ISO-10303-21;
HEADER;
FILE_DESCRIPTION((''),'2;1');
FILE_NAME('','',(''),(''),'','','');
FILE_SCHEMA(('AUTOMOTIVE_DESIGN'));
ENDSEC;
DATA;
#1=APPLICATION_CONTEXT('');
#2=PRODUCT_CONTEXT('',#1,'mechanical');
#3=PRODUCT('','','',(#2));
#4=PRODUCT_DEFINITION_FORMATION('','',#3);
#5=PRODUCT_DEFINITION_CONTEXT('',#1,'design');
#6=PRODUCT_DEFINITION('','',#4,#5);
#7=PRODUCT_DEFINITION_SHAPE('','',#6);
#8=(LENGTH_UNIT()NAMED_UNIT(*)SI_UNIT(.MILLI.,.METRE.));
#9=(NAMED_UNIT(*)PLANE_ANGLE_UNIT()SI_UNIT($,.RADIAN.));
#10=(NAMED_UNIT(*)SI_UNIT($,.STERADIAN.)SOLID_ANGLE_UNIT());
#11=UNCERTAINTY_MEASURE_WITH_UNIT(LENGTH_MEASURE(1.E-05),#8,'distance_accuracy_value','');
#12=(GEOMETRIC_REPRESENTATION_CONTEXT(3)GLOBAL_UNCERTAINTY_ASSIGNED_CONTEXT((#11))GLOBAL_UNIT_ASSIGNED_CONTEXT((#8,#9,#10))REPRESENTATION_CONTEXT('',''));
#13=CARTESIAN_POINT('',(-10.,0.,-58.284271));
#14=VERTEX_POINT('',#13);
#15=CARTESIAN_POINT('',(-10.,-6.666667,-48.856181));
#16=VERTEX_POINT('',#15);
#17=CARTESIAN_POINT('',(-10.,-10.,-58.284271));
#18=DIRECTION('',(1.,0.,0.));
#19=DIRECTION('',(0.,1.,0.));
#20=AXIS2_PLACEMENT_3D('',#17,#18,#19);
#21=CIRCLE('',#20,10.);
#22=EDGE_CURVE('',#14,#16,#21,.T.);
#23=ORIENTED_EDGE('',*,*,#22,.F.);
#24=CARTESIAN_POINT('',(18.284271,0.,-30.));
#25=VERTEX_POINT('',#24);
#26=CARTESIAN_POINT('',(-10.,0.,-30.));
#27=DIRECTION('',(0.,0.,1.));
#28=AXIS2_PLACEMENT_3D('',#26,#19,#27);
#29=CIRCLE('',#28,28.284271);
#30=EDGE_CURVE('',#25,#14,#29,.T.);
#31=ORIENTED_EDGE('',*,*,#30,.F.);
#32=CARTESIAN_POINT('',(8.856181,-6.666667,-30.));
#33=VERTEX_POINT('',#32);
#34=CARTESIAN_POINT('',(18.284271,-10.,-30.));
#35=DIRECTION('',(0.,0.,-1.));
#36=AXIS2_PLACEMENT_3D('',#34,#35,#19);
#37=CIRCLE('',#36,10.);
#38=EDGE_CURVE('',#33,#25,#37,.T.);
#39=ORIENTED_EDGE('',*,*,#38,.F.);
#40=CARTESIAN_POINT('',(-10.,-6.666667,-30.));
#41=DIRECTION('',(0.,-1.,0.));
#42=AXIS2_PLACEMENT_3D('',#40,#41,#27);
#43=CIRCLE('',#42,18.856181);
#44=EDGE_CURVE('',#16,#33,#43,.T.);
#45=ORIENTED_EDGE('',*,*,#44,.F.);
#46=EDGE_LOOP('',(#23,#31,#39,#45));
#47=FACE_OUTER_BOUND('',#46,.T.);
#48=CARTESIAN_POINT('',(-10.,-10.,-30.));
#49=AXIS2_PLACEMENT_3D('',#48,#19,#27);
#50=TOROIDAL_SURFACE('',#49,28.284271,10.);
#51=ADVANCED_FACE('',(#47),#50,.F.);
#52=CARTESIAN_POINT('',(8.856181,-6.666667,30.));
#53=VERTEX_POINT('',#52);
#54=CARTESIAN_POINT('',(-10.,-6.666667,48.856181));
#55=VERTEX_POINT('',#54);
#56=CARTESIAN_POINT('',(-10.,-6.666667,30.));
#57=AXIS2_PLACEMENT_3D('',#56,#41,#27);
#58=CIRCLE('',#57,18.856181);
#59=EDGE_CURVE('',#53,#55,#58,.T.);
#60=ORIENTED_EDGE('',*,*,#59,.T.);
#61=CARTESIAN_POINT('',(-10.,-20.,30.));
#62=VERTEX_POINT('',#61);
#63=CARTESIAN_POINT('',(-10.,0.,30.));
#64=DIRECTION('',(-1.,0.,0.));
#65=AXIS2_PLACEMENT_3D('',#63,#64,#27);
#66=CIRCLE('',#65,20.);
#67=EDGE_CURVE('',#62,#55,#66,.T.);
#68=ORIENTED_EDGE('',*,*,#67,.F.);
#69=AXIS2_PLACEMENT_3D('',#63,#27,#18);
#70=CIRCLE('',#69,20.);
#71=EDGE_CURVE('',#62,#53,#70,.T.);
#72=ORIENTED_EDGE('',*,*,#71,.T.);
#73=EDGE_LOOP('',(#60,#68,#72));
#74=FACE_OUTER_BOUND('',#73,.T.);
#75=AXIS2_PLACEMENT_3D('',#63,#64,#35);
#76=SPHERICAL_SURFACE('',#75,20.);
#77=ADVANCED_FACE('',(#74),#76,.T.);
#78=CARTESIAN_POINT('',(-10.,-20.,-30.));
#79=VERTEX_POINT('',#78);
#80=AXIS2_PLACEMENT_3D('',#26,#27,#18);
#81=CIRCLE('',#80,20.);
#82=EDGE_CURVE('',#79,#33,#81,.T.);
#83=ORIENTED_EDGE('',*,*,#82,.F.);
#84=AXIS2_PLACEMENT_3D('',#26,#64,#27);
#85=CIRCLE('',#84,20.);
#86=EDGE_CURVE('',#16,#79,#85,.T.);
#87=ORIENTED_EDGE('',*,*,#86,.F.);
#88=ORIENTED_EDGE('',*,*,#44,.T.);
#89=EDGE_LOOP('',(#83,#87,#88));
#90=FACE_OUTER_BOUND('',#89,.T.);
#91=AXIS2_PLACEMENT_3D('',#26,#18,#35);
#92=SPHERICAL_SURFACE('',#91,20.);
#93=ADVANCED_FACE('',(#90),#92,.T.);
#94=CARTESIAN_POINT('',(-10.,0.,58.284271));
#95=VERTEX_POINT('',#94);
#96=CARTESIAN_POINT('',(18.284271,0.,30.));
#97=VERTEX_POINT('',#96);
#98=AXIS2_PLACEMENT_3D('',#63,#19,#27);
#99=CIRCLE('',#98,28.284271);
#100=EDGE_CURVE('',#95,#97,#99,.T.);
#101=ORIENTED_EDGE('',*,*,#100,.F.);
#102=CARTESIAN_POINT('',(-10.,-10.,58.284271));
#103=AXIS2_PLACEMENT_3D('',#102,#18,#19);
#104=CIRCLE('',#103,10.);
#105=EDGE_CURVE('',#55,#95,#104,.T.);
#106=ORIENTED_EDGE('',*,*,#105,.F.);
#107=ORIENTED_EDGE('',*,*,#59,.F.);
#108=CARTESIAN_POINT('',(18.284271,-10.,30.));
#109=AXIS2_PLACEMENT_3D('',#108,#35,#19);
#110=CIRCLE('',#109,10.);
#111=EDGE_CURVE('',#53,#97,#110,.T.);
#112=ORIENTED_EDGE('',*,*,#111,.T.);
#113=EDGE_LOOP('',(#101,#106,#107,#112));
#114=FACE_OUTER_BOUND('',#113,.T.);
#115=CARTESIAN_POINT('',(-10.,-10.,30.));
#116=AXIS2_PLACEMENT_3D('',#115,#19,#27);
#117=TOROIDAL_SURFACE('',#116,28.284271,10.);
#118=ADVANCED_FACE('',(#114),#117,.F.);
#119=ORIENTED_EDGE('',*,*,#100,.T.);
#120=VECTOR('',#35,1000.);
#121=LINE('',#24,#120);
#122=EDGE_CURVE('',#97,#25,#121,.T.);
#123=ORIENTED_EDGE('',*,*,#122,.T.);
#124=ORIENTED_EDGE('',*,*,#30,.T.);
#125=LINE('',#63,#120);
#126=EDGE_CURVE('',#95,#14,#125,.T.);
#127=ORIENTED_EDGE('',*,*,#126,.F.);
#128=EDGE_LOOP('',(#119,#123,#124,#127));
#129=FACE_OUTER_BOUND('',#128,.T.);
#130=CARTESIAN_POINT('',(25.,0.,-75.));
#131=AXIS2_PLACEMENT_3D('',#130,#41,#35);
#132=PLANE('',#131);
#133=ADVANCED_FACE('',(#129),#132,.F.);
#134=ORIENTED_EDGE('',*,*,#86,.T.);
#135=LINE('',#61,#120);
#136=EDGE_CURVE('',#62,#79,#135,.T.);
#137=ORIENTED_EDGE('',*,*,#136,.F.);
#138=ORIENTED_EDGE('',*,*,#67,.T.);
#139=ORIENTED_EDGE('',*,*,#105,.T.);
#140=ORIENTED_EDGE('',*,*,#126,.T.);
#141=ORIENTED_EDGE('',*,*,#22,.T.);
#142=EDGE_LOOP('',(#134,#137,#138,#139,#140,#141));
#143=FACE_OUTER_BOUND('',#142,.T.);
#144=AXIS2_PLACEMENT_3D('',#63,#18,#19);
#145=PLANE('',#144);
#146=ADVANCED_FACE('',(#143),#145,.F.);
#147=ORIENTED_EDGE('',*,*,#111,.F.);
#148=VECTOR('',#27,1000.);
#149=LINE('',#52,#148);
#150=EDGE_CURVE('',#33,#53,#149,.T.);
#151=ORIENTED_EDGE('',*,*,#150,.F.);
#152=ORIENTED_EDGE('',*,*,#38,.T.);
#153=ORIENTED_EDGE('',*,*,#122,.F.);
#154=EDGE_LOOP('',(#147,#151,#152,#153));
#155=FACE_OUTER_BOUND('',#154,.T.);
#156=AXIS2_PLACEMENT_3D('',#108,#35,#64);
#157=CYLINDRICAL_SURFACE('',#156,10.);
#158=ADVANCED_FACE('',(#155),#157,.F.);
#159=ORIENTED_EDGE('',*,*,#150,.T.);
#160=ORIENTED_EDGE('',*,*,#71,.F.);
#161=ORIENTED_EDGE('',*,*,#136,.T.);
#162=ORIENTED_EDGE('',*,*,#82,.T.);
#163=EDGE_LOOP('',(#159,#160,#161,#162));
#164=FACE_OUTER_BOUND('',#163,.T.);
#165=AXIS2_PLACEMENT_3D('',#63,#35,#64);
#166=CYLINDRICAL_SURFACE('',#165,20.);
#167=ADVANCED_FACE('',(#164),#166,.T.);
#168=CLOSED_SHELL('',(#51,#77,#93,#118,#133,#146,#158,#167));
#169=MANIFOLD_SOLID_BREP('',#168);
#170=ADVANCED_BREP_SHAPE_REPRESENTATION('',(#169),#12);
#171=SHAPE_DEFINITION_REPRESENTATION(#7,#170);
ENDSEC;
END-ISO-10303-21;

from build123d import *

# Parameters (mm, degrees)
BASE_PROFILE_SKETCH_W          = 50
BASE_PROFILE_SKETCH_H          = 3.464243611
BASE_EXTRUSION_150_DEPTH       = 75
LOUVER_BOSS_DEPTH              = 30
UPPER_CURL_REVOLVE_90DEG_ANGLE = 90
LOWER_CURL_REVOLVE_90DEG_ANGLE = 90
BOTTOM_FILLET_R10_R            = 10
TRIM_CUT_PROFILE_W             = 150
TRIM_CUT_PROFILE_H             = 3.464243611
LOUVER_TRIM_CUT_DEPTH          = 93.33092672


with BuildPart() as part:
    # Base Profile Sketch → Base Extrusion 150 (new, symmetric)
    with BuildSketch(Plane.XY):
        with Locations((0, 1.732121806)):
            Rectangle(BASE_PROFILE_SKETCH_W, BASE_PROFILE_SKETCH_H)
    extrude(amount=BASE_EXTRUSION_150_DEPTH, both=True)

    # Louver Body → Louver Boss (add, symmetric)
    with BuildSketch(Plane.XY):
        with BuildLine():
            Line((-10, 0), (-10, -20))
            ThreePointArc((-10, -20), (4.142135624, -14.142135624), (10, 0))
            Line((10, 0), (-10, 0))
        make_face()
    extrude(amount=LOUVER_BOSS_DEPTH, both=True)

    # Upper Curl Profile → Upper Curl Revolve 90deg (revolve)
    with BuildSketch(Plane.XY.offset(30)):
        with BuildLine():
            Line((10, 0), (-10, 0))
            Line((-10, 0), (-10, -20))
            ThreePointArc((-10, -20), (4.142135624, -14.142135624), (10, 0))
        make_face()
    revolve(axis=Axis((-10, 0, 30), (0, -1, 0)), revolution_arc=UPPER_CURL_REVOLVE_90DEG_ANGLE)

    # Lower Curl Profile → Lower Curl Revolve 90deg (revolve)
    with BuildSketch(Plane(origin=(0, 0, -30), x_dir=(-1, 0, 0), z_dir=(0, 0, -1))):
        with BuildLine():
            Line((10, 0), (-10, 0))
            ThreePointArc((-10, 0), (-4.142135624, -14.142135624), (10, -20))
            Line((10, -20), (10, 0))
        make_face()
    revolve(axis=Axis((-10, -20, -30), (0, 1, 0)), revolution_arc=LOWER_CURL_REVOLVE_90DEG_ANGLE)

    # Bottom Fillet R10
    bottom_fillet_r10_edges = [part.edges().sort_by_distance(p)[0] for p in [
        (10, 0, 0),
        (4.142135624, 0, 44.142135624),
        (4.142135624, 0, -44.142135624),
    ]]
    fillet(bottom_fillet_r10_edges, radius=BOTTOM_FILLET_R10_R)

    # Trim Cut Profile → Louver Trim Cut (cut, through all)
    with BuildSketch(Plane.ZY.offset(25)):
        with Locations((0, 1.732121806)):
            Rectangle(TRIM_CUT_PROFILE_W, TRIM_CUT_PROFILE_H)
    extrude(amount=-LOUVER_TRIM_CUT_DEPTH, mode=Mode.SUBTRACT)


solid = part.part
